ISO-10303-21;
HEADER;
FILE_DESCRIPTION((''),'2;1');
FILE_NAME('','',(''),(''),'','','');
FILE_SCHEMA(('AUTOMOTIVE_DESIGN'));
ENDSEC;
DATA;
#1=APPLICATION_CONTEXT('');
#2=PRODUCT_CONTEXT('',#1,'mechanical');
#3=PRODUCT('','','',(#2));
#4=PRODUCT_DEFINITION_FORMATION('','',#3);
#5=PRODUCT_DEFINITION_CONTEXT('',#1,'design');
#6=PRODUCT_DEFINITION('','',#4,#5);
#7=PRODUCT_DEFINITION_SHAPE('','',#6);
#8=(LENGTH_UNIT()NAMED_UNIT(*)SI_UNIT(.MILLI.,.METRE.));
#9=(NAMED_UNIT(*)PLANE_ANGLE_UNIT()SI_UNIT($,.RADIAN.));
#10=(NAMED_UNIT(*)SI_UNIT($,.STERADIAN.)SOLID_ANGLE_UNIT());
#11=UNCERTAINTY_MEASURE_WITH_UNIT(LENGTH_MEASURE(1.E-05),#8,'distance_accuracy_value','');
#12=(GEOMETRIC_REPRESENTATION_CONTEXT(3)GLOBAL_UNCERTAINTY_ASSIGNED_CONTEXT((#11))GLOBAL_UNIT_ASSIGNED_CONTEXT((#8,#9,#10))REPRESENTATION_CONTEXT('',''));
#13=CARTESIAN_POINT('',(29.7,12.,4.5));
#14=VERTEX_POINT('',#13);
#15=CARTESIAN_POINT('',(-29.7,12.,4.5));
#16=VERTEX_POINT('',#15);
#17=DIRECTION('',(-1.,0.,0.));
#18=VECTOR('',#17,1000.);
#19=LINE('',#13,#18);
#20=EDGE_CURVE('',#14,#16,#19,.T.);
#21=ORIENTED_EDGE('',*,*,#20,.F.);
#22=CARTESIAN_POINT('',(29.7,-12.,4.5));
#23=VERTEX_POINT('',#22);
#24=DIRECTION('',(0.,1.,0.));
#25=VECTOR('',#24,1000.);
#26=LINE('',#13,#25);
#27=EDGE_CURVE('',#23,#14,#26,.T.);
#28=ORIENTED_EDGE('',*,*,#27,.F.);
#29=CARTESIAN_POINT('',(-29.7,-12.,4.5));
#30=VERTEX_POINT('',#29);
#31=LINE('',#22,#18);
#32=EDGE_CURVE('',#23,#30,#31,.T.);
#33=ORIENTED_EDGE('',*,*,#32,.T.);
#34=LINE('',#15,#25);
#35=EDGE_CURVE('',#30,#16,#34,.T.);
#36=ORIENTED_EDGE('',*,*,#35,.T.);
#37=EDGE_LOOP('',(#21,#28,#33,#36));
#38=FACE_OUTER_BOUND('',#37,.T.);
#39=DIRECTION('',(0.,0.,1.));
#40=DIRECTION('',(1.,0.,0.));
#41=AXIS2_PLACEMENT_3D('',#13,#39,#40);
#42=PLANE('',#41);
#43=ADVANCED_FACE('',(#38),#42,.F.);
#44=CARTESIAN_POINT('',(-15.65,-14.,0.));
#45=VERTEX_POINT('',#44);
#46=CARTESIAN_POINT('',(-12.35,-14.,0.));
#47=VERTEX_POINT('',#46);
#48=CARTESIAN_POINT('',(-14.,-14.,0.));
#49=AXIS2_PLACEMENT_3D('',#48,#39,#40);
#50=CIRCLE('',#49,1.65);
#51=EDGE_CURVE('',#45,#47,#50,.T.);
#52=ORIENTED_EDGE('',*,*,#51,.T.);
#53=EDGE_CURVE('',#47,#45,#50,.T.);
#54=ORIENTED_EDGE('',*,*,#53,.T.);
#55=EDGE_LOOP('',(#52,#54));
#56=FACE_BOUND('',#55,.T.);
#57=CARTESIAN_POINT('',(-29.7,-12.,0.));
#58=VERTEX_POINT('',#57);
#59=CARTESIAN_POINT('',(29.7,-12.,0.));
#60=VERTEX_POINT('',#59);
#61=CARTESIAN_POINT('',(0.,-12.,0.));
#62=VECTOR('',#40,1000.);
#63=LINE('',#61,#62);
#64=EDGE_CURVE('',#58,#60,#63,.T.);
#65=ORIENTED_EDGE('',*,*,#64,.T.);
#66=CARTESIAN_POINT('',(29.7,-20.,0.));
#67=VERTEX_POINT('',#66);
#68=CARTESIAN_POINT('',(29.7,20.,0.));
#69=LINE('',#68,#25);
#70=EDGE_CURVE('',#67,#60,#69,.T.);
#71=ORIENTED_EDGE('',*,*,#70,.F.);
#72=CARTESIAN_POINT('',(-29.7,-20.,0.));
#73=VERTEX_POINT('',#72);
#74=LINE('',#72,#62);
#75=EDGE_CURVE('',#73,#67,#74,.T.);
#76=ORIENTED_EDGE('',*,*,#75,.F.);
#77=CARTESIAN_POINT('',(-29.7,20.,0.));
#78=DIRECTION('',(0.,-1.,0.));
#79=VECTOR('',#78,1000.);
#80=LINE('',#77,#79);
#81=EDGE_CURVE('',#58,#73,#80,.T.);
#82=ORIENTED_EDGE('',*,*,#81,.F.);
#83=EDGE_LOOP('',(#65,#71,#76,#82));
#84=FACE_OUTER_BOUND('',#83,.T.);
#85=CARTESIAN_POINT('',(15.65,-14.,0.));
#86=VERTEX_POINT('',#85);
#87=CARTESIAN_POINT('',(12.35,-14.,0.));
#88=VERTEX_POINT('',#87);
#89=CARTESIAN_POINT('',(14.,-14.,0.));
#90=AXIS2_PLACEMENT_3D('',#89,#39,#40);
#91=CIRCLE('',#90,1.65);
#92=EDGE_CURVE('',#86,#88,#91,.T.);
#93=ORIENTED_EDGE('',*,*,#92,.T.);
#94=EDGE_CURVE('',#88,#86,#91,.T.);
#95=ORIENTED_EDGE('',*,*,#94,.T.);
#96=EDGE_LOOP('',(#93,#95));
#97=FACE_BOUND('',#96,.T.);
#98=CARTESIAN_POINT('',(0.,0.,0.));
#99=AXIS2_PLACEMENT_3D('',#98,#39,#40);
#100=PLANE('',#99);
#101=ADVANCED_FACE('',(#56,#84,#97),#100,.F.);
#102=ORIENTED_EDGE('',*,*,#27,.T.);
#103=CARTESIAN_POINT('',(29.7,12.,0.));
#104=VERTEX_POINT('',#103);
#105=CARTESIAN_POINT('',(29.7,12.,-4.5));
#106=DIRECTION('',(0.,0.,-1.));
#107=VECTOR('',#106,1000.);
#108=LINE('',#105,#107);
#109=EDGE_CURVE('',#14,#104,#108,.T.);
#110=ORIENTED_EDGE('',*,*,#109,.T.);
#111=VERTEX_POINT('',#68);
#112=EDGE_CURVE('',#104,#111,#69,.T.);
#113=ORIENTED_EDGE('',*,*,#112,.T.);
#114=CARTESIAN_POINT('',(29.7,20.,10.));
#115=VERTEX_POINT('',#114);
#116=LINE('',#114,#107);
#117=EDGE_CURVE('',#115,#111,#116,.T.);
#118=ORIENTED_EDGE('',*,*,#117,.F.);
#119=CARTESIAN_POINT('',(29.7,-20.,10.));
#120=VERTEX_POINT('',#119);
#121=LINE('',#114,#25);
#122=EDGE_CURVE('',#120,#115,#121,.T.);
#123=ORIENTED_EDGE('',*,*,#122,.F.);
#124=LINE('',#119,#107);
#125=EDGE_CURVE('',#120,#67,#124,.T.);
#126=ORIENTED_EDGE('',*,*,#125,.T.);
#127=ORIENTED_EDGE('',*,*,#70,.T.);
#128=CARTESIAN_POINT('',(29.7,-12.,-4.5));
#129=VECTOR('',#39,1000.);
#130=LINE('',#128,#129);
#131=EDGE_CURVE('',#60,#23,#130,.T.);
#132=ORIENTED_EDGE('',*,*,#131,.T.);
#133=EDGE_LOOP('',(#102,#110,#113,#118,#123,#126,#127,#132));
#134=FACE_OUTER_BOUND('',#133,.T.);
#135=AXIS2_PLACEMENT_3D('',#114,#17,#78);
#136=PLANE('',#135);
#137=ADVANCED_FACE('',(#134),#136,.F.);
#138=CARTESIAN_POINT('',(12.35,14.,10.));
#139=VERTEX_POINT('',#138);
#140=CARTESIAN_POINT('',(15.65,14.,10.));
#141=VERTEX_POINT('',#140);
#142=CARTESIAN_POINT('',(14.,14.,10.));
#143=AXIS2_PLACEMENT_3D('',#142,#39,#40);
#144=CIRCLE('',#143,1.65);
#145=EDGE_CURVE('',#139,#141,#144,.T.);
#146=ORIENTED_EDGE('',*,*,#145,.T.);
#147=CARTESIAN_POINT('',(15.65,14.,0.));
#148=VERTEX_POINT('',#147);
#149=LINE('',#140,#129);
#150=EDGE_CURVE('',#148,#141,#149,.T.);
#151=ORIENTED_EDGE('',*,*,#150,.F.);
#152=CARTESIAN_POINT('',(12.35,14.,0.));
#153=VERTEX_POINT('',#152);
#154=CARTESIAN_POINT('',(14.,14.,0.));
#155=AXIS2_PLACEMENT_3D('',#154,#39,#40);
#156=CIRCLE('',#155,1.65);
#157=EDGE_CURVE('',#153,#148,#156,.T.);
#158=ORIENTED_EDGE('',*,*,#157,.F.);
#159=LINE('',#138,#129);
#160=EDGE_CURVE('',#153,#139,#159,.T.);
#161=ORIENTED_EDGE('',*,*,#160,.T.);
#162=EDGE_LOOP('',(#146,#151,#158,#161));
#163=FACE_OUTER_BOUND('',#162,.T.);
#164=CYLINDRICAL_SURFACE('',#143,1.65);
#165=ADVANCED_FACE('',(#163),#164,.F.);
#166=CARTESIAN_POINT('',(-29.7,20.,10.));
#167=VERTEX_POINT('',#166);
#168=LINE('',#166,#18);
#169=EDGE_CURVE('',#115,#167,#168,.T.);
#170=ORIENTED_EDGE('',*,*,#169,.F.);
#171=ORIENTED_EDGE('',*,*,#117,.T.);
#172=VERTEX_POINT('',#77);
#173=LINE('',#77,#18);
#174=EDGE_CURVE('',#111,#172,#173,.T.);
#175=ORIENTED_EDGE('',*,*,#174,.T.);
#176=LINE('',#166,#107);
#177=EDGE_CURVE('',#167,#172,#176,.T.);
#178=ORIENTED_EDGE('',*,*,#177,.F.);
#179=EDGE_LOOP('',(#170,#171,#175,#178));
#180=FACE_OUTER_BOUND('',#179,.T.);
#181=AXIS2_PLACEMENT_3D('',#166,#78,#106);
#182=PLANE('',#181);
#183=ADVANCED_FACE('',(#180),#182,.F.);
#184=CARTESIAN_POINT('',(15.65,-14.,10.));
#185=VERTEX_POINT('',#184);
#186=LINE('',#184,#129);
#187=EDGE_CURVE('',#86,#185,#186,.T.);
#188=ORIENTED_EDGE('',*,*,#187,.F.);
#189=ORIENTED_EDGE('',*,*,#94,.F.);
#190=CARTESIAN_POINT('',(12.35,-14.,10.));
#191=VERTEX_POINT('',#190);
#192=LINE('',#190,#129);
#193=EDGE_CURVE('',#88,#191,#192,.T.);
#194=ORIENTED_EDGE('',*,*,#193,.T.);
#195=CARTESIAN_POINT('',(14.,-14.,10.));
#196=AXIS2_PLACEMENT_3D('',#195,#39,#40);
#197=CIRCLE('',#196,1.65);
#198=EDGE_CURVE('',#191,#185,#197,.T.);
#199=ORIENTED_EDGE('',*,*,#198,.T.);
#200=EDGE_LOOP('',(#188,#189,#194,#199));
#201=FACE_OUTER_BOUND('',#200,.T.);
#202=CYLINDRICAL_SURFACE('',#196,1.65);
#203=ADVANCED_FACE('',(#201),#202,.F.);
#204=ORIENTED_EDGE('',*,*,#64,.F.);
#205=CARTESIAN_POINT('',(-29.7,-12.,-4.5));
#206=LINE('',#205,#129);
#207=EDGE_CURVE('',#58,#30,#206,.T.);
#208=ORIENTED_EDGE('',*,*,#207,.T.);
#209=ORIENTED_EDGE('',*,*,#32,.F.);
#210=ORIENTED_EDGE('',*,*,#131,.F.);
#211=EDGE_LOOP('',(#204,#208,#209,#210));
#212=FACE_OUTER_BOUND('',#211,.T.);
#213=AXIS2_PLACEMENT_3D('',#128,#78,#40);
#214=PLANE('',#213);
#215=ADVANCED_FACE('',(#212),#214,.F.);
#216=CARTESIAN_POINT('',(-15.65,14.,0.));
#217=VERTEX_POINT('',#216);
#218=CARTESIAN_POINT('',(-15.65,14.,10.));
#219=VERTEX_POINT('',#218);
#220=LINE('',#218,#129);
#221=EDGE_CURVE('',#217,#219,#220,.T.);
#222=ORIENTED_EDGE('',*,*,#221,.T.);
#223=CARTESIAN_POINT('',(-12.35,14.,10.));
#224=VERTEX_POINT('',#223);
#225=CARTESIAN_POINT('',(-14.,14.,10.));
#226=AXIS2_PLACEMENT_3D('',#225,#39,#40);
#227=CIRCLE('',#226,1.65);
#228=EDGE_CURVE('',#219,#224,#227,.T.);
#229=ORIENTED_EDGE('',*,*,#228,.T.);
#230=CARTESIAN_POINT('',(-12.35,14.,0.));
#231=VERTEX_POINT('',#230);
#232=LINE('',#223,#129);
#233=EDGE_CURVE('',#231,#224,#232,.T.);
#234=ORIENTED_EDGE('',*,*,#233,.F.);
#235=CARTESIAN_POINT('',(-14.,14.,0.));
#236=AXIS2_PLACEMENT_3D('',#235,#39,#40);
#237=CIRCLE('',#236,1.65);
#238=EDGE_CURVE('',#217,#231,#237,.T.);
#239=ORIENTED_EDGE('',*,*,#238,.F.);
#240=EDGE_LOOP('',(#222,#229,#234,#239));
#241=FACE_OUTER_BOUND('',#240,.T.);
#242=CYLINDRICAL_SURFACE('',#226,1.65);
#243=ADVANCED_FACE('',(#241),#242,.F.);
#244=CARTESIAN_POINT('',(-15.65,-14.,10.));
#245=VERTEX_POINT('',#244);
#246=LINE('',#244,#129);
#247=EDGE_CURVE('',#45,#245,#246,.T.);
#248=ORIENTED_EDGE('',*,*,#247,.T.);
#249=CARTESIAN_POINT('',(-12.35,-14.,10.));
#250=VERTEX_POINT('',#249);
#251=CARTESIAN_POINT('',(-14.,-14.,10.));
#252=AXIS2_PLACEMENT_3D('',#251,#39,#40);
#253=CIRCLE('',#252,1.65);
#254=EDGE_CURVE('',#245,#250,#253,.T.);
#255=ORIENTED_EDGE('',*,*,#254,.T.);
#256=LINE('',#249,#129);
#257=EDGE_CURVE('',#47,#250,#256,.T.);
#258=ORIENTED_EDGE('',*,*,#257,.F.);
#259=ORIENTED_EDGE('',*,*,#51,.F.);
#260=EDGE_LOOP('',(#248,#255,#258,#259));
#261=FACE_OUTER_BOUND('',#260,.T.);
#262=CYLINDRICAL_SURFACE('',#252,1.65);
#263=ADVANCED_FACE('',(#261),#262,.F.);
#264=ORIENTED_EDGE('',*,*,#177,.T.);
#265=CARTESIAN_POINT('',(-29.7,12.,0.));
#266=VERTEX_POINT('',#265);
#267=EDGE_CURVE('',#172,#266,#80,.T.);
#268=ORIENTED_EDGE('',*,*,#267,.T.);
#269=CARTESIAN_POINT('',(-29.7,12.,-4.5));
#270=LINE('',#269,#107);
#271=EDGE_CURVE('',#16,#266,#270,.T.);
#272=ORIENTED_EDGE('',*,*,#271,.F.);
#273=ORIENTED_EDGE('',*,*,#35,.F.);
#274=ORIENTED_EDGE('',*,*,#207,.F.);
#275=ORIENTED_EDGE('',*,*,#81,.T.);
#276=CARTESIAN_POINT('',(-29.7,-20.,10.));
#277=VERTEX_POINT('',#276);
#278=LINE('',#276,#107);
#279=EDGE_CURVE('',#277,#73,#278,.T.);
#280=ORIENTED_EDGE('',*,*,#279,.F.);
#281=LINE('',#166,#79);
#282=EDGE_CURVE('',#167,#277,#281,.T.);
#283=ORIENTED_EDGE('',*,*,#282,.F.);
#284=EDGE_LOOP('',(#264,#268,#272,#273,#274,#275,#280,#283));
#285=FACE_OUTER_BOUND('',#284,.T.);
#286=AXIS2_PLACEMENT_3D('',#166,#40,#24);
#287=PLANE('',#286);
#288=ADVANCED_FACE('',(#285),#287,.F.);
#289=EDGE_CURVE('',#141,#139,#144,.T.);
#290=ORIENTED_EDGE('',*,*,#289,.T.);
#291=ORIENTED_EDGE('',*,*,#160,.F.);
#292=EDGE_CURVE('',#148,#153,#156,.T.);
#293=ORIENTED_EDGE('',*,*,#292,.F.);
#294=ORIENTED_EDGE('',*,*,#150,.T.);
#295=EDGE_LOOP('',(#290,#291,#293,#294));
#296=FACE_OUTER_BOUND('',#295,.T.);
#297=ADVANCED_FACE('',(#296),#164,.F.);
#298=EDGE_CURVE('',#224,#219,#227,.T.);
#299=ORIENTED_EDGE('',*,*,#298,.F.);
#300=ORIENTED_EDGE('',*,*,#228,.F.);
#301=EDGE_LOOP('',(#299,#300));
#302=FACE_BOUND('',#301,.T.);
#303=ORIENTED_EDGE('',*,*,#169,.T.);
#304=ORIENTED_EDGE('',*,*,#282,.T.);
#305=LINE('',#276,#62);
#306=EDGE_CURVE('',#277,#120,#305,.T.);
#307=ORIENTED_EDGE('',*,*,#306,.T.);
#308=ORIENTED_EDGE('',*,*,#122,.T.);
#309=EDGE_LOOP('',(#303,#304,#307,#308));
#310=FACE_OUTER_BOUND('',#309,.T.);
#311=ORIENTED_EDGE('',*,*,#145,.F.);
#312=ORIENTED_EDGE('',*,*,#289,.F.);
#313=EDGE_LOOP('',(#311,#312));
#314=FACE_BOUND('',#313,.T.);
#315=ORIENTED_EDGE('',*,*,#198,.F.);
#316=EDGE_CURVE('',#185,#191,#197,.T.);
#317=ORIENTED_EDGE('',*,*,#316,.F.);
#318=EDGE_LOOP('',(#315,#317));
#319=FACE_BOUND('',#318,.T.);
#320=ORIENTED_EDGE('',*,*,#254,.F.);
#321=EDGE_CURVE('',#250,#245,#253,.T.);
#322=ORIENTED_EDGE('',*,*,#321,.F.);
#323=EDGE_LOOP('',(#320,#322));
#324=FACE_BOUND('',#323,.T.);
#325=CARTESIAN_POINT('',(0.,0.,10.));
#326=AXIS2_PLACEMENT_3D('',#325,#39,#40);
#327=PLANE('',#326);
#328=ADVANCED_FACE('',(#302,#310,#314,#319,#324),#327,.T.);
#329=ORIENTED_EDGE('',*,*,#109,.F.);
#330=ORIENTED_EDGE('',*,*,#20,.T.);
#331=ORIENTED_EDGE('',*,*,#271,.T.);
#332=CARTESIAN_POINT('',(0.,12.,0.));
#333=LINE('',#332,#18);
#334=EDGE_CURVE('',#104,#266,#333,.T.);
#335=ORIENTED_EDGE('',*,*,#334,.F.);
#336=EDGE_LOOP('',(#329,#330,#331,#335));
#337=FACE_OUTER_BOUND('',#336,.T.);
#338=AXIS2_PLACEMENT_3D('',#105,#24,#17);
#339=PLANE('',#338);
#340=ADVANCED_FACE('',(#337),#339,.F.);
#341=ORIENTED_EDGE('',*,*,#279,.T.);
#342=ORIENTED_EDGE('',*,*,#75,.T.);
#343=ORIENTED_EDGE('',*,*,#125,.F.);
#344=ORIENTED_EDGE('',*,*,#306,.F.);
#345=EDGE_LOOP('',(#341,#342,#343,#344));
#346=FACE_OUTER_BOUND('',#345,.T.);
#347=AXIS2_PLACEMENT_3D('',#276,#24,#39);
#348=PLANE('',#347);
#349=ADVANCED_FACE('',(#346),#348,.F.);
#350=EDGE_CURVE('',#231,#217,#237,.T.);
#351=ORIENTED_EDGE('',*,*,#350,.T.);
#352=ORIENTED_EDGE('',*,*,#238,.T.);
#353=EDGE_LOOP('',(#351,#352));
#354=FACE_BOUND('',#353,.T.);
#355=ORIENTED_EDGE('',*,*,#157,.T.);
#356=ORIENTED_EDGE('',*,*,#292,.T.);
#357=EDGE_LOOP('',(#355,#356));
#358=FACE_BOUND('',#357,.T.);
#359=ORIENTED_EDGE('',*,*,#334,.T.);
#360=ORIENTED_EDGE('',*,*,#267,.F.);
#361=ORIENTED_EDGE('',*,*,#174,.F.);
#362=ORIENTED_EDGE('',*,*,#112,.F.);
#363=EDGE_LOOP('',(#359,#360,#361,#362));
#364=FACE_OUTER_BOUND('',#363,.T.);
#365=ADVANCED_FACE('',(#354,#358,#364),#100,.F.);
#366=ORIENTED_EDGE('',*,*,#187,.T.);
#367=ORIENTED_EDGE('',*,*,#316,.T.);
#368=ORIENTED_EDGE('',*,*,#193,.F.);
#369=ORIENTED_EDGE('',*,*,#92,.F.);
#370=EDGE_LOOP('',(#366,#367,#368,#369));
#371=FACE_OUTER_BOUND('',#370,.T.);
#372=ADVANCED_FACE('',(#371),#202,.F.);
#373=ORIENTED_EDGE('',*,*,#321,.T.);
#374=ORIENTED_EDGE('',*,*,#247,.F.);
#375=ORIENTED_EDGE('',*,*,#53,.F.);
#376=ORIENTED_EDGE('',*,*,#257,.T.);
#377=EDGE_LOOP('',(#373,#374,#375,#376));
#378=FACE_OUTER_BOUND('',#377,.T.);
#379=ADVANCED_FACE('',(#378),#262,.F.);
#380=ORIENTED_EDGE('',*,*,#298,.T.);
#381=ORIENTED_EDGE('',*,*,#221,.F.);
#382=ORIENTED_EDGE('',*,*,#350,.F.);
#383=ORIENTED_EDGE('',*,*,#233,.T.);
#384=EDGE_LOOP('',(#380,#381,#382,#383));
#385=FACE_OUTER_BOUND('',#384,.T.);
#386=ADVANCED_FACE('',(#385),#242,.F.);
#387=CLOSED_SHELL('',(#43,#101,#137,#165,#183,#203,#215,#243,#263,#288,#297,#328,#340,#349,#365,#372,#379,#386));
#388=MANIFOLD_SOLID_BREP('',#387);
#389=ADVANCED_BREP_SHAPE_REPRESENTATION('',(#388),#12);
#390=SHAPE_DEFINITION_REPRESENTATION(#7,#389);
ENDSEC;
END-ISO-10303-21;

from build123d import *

# Parameters (mm, degrees)
SKETCH1_W             = 59.4
SKETCH1_H             = 40
BOSS_EXTRUDE1_DEPTH   = 10
SKETCH2_W             = 9
SKETCH2_H             = 24
CUT_EXTRUDE1_DEPTH    = 64.469362688
M4_TAPPED_HOLE1_D     = 3.3
M4_TAPPED_HOLE1_DEPTH = 10.1
M4_TAPPED_HOLE1_TIP   = 0.991420021


with BuildPart() as part:
    # Sketch1 → Boss-Extrude1 (new body)
    with BuildSketch(Plane.XY):
        Rectangle(SKETCH1_W, SKETCH1_H)
    extrude(amount=BOSS_EXTRUDE1_DEPTH)

    # Sketch2 → Cut-Extrude1 (cut, through all)
    with BuildSketch(Plane.ZY.offset(29.7)):
        Rectangle(SKETCH2_W, SKETCH2_H)
    extrude(amount=-CUT_EXTRUDE1_DEPTH, mode=Mode.SUBTRACT)

    # M4 Tapped Hole1
    with Locations(Plane.XY.offset(10)):
        with Locations((-14, 14), (14, 14), (14, -14), (-14, -14)):
            Hole(M4_TAPPED_HOLE1_D / 2, depth=M4_TAPPED_HOLE1_DEPTH)
            with Locations((0, 0, -(M4_TAPPED_HOLE1_DEPTH + M4_TAPPED_HOLE1_TIP / 2))):  # 118° drill point
                Cone(0, M4_TAPPED_HOLE1_D / 2, M4_TAPPED_HOLE1_TIP, mode=Mode.SUBTRACT)


solid = part.part
